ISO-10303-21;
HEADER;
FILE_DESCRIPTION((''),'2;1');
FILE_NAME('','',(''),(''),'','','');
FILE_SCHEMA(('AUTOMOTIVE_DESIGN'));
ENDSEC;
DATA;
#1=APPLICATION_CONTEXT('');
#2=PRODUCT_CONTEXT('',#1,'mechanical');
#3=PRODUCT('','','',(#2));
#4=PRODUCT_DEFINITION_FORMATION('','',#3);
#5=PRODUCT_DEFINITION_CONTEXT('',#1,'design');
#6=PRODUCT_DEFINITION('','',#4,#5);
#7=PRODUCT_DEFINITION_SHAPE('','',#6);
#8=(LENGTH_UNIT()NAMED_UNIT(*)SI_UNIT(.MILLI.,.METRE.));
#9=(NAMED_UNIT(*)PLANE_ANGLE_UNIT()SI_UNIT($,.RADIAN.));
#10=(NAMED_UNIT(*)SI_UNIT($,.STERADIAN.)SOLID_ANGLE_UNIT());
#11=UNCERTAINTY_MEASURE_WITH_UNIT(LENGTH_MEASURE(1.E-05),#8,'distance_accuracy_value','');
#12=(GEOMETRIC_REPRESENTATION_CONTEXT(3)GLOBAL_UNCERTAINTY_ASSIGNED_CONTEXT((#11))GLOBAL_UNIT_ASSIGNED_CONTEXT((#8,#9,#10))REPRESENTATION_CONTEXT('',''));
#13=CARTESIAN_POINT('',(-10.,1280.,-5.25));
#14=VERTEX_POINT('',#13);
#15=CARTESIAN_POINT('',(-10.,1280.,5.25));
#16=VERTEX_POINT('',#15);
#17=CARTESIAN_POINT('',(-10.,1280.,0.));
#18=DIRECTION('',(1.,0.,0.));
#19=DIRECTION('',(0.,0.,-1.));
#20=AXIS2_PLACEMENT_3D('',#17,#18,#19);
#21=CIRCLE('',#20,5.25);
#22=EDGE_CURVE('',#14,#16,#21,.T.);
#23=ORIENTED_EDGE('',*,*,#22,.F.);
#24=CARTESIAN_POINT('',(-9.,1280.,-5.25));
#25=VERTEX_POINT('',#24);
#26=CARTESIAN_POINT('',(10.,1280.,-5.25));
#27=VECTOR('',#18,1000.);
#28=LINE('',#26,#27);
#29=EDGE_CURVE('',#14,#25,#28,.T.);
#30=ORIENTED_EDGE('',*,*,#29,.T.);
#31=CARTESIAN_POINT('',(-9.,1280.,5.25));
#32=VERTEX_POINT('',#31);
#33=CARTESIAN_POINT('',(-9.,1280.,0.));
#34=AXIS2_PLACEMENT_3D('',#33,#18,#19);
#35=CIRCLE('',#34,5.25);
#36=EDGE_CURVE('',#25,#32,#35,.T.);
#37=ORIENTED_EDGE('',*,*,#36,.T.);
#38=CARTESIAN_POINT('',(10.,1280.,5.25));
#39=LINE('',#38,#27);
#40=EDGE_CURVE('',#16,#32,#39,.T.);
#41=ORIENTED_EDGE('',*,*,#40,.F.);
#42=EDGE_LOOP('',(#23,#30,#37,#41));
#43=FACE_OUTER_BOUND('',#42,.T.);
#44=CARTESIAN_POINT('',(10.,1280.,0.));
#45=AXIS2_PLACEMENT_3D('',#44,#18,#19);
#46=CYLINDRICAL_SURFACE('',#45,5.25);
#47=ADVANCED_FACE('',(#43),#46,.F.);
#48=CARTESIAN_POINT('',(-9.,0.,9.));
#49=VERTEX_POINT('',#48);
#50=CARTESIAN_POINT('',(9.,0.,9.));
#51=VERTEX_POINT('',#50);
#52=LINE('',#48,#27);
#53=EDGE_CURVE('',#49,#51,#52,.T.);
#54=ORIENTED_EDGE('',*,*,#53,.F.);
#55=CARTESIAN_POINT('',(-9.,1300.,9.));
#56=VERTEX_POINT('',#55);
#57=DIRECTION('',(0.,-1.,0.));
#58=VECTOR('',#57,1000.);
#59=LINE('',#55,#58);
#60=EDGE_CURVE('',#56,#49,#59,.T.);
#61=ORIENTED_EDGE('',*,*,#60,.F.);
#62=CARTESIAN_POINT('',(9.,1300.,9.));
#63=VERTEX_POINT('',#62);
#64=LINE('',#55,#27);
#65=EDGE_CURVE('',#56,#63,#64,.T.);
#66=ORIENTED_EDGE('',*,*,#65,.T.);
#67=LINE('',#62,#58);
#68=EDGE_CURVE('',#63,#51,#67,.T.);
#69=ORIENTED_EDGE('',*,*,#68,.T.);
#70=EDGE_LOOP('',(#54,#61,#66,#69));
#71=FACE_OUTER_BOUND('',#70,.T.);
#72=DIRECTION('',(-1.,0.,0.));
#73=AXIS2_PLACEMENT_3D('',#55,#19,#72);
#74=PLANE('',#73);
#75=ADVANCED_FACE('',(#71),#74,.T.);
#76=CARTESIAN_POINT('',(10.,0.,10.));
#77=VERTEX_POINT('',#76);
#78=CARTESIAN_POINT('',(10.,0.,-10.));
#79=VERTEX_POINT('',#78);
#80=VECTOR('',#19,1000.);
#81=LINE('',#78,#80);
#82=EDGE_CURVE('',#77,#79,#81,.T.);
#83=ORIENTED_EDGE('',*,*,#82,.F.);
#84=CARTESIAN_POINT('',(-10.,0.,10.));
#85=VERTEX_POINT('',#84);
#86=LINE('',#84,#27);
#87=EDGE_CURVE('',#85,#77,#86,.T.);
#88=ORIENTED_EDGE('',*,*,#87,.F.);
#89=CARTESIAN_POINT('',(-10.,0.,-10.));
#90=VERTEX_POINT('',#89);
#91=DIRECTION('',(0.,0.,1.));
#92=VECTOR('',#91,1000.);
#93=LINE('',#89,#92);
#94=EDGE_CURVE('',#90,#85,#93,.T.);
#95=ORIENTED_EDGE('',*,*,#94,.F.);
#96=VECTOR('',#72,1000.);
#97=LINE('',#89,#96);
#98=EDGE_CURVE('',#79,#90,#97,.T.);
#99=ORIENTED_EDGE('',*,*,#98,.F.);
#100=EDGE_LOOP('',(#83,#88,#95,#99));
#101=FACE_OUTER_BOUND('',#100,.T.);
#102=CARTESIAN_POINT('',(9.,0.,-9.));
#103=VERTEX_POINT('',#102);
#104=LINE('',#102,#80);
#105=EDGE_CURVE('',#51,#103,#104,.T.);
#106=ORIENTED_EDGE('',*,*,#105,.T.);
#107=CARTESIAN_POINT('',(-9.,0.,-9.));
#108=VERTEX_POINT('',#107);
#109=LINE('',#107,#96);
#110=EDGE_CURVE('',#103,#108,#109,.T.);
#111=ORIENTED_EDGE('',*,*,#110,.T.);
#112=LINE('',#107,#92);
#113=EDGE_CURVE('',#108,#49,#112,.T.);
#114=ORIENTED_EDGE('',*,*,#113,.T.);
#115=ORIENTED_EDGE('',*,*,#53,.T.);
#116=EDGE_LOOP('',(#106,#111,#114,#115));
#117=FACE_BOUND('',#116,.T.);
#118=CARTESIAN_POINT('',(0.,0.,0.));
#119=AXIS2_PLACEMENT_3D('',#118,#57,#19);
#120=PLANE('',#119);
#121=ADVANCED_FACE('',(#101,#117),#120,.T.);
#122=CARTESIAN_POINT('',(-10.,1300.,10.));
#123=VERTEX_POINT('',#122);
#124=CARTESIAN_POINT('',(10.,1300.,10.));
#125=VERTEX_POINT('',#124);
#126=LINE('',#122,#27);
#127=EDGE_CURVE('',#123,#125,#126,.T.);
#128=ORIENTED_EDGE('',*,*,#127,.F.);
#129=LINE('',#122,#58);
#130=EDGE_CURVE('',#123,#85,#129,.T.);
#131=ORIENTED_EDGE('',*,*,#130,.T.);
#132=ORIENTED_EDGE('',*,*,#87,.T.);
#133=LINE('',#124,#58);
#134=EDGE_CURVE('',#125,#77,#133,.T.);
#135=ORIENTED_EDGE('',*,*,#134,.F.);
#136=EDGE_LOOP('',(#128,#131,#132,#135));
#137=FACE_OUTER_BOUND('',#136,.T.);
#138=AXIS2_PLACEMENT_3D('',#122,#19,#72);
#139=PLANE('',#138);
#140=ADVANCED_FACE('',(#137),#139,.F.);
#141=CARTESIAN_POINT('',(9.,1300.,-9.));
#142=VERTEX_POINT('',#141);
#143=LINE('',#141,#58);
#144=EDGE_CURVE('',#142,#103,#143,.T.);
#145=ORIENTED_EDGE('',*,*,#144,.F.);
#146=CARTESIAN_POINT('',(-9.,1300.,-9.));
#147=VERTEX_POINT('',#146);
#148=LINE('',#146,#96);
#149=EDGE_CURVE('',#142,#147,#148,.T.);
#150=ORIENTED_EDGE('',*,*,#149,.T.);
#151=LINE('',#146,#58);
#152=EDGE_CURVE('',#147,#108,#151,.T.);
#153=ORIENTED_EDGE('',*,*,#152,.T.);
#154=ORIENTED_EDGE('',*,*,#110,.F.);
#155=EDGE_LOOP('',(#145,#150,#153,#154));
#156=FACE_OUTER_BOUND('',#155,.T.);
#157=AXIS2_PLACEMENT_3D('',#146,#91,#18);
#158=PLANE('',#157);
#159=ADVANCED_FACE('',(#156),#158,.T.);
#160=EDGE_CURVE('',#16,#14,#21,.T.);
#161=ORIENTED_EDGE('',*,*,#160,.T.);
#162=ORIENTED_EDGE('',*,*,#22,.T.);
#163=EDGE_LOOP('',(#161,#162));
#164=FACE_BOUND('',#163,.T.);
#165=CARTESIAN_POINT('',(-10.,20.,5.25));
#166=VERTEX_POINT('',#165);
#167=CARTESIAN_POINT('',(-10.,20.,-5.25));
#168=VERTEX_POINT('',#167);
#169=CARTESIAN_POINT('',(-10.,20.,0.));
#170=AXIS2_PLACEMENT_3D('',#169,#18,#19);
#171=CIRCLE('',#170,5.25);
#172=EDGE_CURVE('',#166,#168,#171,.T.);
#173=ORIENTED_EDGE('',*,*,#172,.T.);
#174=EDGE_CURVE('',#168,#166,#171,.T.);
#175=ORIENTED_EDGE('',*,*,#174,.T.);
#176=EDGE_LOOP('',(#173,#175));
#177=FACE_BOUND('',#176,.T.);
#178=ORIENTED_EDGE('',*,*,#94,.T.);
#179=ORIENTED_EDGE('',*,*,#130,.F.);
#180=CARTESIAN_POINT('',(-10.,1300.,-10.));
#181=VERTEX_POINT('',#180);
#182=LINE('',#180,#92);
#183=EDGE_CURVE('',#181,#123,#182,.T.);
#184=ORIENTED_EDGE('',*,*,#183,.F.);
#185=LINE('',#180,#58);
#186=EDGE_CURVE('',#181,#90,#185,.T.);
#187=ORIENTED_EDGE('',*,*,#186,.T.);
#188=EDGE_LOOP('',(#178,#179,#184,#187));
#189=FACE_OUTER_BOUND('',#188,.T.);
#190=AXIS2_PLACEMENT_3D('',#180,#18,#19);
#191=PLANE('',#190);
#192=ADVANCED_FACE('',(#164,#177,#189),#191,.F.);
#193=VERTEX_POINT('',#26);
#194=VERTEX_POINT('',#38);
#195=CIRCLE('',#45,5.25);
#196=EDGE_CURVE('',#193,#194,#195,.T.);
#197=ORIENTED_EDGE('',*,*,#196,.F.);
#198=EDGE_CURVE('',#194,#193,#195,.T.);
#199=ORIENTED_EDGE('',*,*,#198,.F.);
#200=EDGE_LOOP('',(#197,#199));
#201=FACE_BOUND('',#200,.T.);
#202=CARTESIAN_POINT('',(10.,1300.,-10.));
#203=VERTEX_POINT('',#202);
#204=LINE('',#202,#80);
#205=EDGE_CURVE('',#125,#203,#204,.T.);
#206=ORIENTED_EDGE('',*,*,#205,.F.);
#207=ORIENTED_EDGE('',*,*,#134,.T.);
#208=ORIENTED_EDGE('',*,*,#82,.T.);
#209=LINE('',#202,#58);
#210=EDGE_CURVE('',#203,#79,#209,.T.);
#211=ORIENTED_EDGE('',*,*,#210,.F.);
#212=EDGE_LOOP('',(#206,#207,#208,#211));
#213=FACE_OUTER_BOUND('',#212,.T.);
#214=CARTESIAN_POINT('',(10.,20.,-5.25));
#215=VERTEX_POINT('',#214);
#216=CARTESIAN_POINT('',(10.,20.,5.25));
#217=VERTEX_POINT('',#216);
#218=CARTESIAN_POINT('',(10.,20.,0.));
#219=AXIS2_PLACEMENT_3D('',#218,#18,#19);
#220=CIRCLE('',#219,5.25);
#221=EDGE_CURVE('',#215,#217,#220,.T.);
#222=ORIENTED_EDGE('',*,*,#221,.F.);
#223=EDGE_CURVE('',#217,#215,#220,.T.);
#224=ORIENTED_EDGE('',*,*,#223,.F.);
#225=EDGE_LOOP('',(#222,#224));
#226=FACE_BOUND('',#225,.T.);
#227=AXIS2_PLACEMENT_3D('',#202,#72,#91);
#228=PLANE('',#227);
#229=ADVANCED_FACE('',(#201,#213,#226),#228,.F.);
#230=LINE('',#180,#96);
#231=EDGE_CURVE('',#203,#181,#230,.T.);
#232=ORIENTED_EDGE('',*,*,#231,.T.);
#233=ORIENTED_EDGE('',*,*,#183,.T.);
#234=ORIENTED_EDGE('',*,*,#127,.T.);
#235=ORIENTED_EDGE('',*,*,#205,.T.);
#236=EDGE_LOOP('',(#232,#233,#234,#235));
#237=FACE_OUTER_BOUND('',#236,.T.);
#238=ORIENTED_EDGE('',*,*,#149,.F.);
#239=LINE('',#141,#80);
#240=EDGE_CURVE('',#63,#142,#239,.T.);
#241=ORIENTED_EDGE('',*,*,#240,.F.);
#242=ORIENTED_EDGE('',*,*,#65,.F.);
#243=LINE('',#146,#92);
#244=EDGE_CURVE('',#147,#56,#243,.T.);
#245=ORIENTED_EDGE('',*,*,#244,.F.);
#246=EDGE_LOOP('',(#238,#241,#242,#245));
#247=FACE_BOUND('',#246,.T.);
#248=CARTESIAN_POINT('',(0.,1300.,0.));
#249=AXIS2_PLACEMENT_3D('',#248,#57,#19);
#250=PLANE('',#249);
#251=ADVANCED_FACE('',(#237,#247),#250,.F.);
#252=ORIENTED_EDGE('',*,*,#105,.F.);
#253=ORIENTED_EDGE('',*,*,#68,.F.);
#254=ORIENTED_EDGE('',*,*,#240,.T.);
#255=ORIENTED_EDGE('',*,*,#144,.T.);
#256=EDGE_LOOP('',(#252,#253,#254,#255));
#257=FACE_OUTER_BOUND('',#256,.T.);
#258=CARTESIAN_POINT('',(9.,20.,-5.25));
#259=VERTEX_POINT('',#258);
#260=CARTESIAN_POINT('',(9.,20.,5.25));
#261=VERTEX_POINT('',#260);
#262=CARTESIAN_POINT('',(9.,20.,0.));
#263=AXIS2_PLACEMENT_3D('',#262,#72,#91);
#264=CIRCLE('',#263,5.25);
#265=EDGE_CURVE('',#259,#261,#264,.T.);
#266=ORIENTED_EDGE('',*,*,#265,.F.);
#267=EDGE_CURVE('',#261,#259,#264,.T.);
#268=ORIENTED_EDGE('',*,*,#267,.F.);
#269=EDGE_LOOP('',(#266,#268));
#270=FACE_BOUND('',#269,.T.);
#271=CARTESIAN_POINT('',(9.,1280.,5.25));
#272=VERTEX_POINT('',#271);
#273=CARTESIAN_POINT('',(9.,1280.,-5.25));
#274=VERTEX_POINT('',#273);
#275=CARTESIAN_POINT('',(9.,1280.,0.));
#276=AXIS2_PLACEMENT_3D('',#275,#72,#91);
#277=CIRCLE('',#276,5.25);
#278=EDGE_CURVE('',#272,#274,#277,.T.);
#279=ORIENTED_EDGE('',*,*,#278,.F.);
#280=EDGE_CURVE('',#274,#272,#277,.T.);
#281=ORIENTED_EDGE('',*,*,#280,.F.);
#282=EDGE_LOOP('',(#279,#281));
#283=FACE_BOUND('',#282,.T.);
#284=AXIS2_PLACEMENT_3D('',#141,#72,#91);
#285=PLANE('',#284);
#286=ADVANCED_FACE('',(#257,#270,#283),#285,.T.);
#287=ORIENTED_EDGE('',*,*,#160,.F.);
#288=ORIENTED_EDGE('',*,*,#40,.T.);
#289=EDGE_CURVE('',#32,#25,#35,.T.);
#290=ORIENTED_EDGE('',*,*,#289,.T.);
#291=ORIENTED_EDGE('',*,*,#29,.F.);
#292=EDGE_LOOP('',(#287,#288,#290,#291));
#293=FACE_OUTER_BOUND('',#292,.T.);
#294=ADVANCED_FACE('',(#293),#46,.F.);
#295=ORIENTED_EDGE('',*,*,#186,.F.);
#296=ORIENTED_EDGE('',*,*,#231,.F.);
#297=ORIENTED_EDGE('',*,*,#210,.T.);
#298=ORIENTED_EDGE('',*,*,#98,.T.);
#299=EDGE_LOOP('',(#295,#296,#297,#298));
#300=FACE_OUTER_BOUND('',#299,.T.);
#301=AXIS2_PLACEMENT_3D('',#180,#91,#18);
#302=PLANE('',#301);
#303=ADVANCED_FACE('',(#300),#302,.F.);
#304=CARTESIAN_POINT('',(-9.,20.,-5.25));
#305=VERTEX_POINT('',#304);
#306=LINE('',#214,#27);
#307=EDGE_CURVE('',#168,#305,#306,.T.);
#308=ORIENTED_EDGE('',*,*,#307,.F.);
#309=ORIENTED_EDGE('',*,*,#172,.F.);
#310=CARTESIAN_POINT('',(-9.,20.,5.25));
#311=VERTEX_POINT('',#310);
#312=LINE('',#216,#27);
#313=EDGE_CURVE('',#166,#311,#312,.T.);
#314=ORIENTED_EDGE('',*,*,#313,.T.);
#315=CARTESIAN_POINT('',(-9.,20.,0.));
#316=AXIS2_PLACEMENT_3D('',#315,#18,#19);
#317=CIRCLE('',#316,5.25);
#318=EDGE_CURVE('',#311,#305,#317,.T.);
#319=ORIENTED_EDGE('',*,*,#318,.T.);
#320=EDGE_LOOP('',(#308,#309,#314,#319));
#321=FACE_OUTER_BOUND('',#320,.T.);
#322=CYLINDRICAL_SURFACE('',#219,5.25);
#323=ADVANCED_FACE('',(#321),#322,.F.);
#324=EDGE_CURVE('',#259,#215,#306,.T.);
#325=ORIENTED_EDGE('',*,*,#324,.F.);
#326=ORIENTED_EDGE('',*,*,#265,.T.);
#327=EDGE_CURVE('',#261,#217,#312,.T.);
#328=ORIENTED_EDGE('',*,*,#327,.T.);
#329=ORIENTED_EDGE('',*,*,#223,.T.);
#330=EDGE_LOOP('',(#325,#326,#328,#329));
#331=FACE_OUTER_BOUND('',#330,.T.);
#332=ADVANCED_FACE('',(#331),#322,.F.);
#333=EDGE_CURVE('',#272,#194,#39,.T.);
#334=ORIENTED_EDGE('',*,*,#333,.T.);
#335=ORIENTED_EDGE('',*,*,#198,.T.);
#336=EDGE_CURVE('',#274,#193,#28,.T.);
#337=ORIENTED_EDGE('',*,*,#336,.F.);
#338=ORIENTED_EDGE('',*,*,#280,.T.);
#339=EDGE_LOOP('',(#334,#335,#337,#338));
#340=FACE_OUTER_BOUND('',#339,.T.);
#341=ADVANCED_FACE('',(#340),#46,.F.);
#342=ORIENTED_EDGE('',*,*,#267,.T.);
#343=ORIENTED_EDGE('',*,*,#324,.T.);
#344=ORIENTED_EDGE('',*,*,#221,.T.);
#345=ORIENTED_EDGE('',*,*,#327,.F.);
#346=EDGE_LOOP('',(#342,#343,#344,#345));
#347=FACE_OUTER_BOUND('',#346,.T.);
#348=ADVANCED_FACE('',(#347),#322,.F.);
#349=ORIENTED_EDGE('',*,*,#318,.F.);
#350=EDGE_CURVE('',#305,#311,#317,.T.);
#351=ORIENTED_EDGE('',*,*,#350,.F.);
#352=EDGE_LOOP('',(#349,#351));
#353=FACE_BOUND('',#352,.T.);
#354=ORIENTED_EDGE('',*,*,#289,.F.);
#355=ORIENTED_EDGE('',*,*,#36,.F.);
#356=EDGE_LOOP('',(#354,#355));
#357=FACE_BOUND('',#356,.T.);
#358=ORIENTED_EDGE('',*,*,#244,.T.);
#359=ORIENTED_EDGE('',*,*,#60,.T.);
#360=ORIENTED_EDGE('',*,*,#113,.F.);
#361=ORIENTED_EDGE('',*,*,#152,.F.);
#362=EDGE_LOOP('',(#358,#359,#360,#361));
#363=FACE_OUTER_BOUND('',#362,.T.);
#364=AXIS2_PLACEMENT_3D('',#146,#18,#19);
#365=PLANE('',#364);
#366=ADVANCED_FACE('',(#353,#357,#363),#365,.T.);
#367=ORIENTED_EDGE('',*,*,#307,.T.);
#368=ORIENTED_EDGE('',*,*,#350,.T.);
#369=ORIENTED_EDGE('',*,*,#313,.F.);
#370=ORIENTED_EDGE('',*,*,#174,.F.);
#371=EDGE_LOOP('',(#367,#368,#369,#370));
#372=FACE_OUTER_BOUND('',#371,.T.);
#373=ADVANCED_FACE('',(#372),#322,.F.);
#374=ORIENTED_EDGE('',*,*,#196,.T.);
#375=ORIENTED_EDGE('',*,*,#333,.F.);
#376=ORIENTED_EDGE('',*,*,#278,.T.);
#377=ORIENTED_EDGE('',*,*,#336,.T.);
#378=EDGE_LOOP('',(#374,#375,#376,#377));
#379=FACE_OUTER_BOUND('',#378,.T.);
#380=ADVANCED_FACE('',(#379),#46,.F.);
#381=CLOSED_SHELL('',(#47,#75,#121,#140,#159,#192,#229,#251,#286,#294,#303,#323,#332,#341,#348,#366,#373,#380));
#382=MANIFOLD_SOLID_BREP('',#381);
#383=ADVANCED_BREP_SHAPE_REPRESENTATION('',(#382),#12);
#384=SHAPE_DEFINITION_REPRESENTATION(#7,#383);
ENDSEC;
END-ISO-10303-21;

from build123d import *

# Parameters (mm, degrees)
SKETCH12_W                = 20
SKETCH12_H                = 20
SKETCH12_W_2              = 18
SKETCH12_H_2              = 18
F_20_X_20_X_1_1_DEPTH     = 1300
HOLE_WIZARD_10_5_10_5_1_D = 10.5


with BuildPart() as part:
    # Sketch12 → 方通 20 X 20 X 1(1) (new body)
    with BuildSketch(Plane.ZX):
        Rectangle(SKETCH12_W, SKETCH12_H)
        Rectangle(SKETCH12_W_2, SKETCH12_H_2, mode=Mode.SUBTRACT)
    extrude(amount=F_20_X_20_X_1_1_DEPTH)

    # Ø10.5 (10.5) 直径孔1 (through all)
    with Locations(Plane(origin=(10, 0, 0), x_dir=(0, 0, -1), z_dir=(1, 0, 0))):
        with Locations((0, 20), (0, 1280)):
            Hole(HOLE_WIZARD_10_5_10_5_1_D / 2)


solid = part.part
